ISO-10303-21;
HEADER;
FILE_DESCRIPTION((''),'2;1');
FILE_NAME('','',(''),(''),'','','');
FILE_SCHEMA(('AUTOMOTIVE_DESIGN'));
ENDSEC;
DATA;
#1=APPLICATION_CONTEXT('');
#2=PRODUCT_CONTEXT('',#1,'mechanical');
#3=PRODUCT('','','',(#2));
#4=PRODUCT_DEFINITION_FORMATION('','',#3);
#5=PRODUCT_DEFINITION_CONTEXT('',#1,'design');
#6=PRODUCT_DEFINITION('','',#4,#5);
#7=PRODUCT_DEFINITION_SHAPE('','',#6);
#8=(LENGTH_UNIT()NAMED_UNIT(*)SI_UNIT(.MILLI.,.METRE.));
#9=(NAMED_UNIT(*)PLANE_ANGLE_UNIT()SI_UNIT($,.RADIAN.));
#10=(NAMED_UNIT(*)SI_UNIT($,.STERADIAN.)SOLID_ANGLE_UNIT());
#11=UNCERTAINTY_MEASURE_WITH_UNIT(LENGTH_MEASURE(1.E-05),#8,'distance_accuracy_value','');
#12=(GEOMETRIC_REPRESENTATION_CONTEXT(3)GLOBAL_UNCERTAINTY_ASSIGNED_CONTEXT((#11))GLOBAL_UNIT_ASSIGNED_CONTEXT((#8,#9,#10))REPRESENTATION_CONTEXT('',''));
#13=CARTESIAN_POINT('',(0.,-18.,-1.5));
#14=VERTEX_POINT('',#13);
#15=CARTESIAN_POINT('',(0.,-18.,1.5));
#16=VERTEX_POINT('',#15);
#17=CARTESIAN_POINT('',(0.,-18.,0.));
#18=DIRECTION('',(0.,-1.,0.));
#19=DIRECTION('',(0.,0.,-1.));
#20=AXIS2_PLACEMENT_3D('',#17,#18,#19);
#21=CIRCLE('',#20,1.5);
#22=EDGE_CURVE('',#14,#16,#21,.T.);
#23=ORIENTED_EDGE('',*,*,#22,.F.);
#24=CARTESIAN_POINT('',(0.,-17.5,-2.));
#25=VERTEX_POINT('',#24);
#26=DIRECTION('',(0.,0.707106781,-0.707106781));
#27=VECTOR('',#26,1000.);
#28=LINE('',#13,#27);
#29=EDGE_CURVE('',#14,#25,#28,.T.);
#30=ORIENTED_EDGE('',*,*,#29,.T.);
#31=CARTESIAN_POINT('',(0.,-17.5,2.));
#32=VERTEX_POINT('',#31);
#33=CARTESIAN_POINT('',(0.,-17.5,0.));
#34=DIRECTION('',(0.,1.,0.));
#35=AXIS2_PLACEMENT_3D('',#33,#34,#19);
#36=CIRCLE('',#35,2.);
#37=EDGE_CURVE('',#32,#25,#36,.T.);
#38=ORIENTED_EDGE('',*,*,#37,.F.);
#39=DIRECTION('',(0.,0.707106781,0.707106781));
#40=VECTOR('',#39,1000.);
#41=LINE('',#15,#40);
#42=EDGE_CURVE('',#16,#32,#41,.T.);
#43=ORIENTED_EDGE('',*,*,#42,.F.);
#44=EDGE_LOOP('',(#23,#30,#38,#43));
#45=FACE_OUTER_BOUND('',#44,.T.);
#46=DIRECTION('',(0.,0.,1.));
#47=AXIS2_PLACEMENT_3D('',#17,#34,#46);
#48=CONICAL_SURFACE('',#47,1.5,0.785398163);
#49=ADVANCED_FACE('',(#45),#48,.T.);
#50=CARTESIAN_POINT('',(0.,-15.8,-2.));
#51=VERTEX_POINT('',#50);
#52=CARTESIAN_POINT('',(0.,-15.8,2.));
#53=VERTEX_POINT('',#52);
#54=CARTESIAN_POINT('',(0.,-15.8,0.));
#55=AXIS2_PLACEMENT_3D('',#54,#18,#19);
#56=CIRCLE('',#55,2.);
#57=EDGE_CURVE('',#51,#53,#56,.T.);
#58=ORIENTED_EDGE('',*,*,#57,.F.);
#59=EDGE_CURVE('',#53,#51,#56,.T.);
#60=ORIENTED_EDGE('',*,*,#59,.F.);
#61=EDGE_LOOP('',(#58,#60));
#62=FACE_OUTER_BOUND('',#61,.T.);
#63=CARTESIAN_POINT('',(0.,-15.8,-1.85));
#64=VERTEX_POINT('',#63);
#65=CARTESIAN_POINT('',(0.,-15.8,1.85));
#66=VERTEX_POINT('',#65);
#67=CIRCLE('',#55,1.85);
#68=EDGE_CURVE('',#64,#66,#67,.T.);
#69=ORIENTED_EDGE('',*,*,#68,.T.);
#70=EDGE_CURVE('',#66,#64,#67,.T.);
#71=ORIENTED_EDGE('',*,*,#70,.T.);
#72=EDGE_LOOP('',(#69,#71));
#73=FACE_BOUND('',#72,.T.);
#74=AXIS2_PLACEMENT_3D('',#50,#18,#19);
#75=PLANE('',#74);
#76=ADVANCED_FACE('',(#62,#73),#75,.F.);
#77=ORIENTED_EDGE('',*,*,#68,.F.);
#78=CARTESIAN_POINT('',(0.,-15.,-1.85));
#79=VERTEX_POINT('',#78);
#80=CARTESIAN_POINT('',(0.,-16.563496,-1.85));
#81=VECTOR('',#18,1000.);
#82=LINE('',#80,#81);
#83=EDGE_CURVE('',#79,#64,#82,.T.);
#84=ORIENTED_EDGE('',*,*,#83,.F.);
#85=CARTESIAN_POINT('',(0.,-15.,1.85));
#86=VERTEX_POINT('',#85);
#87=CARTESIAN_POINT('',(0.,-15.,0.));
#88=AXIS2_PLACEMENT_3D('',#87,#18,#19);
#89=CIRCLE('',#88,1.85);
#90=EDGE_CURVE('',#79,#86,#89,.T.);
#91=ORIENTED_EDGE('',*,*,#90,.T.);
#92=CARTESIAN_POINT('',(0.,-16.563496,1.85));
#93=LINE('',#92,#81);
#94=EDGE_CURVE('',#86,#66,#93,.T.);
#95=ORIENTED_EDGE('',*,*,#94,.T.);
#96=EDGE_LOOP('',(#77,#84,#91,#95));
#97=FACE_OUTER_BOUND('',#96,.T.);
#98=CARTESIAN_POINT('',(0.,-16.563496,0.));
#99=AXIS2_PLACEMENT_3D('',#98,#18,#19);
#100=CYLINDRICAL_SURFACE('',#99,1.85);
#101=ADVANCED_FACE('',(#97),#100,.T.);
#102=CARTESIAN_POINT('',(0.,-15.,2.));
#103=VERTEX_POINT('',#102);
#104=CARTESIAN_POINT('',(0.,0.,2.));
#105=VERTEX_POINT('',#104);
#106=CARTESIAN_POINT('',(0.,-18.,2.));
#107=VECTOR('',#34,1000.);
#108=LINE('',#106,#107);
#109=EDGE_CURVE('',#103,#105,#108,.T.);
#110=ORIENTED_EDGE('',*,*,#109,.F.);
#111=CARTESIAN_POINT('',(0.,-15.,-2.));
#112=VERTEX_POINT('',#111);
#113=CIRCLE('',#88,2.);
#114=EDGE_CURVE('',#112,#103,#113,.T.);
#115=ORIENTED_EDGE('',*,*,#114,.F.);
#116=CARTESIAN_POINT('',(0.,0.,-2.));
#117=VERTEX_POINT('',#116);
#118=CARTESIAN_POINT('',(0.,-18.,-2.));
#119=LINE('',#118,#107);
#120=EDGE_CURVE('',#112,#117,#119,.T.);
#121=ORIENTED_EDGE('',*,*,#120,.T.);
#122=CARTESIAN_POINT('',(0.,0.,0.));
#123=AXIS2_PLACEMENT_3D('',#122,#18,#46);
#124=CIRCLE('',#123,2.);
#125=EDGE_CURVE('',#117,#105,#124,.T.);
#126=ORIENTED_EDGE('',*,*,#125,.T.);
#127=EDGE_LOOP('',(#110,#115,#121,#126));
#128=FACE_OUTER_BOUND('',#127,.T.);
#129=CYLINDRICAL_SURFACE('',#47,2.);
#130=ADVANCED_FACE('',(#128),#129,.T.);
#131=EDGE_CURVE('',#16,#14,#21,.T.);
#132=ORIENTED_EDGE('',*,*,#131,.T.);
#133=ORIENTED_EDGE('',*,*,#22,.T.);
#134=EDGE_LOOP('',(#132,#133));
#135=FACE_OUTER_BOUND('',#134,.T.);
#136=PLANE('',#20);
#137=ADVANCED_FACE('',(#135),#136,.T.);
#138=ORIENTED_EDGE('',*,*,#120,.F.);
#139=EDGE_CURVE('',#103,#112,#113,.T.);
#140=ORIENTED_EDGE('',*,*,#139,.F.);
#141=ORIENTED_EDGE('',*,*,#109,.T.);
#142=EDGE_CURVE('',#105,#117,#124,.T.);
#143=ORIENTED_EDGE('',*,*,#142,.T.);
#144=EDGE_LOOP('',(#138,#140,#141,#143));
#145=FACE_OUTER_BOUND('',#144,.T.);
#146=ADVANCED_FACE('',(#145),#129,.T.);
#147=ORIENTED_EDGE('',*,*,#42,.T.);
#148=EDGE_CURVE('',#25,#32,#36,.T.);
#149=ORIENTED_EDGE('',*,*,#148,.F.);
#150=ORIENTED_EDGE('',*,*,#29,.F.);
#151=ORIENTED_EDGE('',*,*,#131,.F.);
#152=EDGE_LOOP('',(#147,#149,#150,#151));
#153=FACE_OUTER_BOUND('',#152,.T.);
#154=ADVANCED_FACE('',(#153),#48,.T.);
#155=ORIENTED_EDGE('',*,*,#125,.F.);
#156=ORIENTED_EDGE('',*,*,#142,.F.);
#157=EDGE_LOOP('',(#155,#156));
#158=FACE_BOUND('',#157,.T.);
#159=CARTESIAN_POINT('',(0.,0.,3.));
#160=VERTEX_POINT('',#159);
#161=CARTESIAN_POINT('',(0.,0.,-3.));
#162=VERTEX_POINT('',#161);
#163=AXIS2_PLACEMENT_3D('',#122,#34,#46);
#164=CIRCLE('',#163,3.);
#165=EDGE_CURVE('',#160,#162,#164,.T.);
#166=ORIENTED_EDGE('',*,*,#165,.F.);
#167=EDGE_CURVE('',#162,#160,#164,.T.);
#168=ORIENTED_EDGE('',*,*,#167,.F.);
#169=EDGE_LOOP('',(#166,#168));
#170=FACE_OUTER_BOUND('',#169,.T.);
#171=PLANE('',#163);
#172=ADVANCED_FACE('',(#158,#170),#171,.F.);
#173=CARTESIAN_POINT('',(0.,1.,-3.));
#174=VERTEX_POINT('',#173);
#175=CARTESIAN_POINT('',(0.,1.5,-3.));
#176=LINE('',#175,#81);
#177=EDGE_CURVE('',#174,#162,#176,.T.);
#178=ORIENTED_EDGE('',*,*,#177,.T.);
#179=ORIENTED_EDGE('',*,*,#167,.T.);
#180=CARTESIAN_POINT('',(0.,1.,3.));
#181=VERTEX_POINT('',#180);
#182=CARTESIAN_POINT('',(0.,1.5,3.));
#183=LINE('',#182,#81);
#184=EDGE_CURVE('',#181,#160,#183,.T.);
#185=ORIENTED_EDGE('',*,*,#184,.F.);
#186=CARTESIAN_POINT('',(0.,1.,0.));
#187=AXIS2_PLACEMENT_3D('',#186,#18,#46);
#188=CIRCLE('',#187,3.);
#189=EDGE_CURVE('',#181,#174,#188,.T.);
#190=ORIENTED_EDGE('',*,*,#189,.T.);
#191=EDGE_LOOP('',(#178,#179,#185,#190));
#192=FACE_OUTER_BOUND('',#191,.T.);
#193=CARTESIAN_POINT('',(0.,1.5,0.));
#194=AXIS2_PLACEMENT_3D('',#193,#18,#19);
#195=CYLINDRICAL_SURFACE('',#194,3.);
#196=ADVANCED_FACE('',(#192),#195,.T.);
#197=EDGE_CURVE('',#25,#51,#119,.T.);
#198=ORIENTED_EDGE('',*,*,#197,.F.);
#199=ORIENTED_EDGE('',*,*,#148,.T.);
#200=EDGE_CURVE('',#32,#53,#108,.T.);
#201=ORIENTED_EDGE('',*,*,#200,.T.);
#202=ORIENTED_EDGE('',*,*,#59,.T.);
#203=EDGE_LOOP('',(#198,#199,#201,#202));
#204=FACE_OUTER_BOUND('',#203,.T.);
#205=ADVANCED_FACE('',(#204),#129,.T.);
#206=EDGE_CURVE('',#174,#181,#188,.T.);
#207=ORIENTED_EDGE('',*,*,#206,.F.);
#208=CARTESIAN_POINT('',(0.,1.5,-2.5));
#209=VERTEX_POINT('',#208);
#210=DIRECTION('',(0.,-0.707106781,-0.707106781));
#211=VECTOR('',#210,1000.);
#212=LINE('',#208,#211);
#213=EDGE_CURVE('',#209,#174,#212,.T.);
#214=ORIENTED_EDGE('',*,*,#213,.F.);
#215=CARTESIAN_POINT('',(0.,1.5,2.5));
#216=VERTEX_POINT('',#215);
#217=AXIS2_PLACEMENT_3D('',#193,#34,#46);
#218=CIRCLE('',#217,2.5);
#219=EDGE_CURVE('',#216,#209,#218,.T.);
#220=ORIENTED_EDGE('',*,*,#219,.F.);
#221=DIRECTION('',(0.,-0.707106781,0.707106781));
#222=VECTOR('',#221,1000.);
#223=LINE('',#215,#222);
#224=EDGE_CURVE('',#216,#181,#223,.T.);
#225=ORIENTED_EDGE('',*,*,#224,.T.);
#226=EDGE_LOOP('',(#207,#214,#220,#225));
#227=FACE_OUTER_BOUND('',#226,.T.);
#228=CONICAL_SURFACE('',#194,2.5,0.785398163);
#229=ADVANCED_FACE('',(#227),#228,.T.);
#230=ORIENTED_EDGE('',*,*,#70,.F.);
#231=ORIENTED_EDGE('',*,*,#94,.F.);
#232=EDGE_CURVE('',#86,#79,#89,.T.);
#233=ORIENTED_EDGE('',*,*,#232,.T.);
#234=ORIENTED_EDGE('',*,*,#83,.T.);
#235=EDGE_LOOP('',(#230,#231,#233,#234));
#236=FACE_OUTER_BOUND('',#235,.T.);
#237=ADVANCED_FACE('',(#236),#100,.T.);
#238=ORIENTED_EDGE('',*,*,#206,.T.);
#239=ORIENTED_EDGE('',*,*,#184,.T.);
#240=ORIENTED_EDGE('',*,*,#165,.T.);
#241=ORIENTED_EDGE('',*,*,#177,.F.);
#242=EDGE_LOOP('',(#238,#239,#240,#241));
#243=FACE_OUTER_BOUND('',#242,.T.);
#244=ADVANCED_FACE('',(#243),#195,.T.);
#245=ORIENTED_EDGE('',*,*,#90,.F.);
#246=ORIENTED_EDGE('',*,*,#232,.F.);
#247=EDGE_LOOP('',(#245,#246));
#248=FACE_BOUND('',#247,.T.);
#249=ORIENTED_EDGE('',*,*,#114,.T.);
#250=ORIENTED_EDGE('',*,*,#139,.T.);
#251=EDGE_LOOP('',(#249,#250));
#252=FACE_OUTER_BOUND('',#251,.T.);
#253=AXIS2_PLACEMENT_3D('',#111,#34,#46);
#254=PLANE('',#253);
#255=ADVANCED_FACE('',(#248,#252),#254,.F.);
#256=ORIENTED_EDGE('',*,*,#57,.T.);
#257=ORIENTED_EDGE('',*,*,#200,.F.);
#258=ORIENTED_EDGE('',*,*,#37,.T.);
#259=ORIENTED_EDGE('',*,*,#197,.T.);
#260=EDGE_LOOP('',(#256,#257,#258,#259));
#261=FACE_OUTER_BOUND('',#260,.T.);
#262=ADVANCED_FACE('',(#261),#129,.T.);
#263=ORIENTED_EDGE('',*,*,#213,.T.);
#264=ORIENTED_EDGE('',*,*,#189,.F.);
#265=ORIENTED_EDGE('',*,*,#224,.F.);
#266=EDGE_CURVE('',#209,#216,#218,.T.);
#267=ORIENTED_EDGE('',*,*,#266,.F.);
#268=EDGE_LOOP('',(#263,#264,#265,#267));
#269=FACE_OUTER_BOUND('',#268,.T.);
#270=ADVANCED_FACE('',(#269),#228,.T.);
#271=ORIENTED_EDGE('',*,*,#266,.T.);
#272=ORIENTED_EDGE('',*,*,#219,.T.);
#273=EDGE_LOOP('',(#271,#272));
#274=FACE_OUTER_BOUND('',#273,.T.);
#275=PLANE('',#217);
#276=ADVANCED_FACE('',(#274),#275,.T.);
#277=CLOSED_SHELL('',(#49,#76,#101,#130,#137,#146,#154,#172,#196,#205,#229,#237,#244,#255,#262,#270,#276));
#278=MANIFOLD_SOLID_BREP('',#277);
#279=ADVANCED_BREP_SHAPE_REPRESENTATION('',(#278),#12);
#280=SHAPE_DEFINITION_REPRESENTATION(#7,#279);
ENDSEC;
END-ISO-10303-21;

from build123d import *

# Parameters (mm, degrees)
SKETCH1_R           = 3
BOSS_EXTRUDE1_DEPTH = 1.5
SKETCH2_R           = 2
BOSS_EXTRUDE2_DEPTH = 18
SKETCH3_W           = 0.15
SKETCH3_H           = 0.8
CHAMFER1_SIZE       = 0.5


with BuildPart() as part:
    # Sketch1 → Boss-Extrude1 (new body)
    with BuildSketch(Plane(origin=(0, 0, 0), x_dir=(1, 0, 0), z_dir=(0, 1, 0))):
        with Locations(Location((0, 0, 0), (0, 0, 270))):
            Circle(SKETCH1_R)
    extrude(amount=BOSS_EXTRUDE1_DEPTH)

    # Sketch2 → Boss-Extrude2 (add)
    with BuildSketch(Plane.XZ):
        with Locations(Location((0, 0, 0), (0, 0, 90))):
            Circle(SKETCH2_R)
    extrude(amount=BOSS_EXTRUDE2_DEPTH)

    # Sketch3 → Cut-Revolve1 (revolve, cut)
    with BuildSketch(Plane(origin=(0, 0, 0), x_dir=(0, 0, -1), z_dir=(1, 0, 0))):
        with Locations((1.925, -15.4)):
            Rectangle(SKETCH3_W, SKETCH3_H)
    revolve(axis=Axis((0, -16.563495901, 0), (0, 1, 0)), mode=Mode.SUBTRACT)

    # Chamfer1
    chamfer1_edges = [part.edges().sort_by_distance(p)[0] for p in [
        (0, 1.5, -3),
        (0, -18, -2),
    ]]
    chamfer(chamfer1_edges, length=CHAMFER1_SIZE)


solid = part.part
